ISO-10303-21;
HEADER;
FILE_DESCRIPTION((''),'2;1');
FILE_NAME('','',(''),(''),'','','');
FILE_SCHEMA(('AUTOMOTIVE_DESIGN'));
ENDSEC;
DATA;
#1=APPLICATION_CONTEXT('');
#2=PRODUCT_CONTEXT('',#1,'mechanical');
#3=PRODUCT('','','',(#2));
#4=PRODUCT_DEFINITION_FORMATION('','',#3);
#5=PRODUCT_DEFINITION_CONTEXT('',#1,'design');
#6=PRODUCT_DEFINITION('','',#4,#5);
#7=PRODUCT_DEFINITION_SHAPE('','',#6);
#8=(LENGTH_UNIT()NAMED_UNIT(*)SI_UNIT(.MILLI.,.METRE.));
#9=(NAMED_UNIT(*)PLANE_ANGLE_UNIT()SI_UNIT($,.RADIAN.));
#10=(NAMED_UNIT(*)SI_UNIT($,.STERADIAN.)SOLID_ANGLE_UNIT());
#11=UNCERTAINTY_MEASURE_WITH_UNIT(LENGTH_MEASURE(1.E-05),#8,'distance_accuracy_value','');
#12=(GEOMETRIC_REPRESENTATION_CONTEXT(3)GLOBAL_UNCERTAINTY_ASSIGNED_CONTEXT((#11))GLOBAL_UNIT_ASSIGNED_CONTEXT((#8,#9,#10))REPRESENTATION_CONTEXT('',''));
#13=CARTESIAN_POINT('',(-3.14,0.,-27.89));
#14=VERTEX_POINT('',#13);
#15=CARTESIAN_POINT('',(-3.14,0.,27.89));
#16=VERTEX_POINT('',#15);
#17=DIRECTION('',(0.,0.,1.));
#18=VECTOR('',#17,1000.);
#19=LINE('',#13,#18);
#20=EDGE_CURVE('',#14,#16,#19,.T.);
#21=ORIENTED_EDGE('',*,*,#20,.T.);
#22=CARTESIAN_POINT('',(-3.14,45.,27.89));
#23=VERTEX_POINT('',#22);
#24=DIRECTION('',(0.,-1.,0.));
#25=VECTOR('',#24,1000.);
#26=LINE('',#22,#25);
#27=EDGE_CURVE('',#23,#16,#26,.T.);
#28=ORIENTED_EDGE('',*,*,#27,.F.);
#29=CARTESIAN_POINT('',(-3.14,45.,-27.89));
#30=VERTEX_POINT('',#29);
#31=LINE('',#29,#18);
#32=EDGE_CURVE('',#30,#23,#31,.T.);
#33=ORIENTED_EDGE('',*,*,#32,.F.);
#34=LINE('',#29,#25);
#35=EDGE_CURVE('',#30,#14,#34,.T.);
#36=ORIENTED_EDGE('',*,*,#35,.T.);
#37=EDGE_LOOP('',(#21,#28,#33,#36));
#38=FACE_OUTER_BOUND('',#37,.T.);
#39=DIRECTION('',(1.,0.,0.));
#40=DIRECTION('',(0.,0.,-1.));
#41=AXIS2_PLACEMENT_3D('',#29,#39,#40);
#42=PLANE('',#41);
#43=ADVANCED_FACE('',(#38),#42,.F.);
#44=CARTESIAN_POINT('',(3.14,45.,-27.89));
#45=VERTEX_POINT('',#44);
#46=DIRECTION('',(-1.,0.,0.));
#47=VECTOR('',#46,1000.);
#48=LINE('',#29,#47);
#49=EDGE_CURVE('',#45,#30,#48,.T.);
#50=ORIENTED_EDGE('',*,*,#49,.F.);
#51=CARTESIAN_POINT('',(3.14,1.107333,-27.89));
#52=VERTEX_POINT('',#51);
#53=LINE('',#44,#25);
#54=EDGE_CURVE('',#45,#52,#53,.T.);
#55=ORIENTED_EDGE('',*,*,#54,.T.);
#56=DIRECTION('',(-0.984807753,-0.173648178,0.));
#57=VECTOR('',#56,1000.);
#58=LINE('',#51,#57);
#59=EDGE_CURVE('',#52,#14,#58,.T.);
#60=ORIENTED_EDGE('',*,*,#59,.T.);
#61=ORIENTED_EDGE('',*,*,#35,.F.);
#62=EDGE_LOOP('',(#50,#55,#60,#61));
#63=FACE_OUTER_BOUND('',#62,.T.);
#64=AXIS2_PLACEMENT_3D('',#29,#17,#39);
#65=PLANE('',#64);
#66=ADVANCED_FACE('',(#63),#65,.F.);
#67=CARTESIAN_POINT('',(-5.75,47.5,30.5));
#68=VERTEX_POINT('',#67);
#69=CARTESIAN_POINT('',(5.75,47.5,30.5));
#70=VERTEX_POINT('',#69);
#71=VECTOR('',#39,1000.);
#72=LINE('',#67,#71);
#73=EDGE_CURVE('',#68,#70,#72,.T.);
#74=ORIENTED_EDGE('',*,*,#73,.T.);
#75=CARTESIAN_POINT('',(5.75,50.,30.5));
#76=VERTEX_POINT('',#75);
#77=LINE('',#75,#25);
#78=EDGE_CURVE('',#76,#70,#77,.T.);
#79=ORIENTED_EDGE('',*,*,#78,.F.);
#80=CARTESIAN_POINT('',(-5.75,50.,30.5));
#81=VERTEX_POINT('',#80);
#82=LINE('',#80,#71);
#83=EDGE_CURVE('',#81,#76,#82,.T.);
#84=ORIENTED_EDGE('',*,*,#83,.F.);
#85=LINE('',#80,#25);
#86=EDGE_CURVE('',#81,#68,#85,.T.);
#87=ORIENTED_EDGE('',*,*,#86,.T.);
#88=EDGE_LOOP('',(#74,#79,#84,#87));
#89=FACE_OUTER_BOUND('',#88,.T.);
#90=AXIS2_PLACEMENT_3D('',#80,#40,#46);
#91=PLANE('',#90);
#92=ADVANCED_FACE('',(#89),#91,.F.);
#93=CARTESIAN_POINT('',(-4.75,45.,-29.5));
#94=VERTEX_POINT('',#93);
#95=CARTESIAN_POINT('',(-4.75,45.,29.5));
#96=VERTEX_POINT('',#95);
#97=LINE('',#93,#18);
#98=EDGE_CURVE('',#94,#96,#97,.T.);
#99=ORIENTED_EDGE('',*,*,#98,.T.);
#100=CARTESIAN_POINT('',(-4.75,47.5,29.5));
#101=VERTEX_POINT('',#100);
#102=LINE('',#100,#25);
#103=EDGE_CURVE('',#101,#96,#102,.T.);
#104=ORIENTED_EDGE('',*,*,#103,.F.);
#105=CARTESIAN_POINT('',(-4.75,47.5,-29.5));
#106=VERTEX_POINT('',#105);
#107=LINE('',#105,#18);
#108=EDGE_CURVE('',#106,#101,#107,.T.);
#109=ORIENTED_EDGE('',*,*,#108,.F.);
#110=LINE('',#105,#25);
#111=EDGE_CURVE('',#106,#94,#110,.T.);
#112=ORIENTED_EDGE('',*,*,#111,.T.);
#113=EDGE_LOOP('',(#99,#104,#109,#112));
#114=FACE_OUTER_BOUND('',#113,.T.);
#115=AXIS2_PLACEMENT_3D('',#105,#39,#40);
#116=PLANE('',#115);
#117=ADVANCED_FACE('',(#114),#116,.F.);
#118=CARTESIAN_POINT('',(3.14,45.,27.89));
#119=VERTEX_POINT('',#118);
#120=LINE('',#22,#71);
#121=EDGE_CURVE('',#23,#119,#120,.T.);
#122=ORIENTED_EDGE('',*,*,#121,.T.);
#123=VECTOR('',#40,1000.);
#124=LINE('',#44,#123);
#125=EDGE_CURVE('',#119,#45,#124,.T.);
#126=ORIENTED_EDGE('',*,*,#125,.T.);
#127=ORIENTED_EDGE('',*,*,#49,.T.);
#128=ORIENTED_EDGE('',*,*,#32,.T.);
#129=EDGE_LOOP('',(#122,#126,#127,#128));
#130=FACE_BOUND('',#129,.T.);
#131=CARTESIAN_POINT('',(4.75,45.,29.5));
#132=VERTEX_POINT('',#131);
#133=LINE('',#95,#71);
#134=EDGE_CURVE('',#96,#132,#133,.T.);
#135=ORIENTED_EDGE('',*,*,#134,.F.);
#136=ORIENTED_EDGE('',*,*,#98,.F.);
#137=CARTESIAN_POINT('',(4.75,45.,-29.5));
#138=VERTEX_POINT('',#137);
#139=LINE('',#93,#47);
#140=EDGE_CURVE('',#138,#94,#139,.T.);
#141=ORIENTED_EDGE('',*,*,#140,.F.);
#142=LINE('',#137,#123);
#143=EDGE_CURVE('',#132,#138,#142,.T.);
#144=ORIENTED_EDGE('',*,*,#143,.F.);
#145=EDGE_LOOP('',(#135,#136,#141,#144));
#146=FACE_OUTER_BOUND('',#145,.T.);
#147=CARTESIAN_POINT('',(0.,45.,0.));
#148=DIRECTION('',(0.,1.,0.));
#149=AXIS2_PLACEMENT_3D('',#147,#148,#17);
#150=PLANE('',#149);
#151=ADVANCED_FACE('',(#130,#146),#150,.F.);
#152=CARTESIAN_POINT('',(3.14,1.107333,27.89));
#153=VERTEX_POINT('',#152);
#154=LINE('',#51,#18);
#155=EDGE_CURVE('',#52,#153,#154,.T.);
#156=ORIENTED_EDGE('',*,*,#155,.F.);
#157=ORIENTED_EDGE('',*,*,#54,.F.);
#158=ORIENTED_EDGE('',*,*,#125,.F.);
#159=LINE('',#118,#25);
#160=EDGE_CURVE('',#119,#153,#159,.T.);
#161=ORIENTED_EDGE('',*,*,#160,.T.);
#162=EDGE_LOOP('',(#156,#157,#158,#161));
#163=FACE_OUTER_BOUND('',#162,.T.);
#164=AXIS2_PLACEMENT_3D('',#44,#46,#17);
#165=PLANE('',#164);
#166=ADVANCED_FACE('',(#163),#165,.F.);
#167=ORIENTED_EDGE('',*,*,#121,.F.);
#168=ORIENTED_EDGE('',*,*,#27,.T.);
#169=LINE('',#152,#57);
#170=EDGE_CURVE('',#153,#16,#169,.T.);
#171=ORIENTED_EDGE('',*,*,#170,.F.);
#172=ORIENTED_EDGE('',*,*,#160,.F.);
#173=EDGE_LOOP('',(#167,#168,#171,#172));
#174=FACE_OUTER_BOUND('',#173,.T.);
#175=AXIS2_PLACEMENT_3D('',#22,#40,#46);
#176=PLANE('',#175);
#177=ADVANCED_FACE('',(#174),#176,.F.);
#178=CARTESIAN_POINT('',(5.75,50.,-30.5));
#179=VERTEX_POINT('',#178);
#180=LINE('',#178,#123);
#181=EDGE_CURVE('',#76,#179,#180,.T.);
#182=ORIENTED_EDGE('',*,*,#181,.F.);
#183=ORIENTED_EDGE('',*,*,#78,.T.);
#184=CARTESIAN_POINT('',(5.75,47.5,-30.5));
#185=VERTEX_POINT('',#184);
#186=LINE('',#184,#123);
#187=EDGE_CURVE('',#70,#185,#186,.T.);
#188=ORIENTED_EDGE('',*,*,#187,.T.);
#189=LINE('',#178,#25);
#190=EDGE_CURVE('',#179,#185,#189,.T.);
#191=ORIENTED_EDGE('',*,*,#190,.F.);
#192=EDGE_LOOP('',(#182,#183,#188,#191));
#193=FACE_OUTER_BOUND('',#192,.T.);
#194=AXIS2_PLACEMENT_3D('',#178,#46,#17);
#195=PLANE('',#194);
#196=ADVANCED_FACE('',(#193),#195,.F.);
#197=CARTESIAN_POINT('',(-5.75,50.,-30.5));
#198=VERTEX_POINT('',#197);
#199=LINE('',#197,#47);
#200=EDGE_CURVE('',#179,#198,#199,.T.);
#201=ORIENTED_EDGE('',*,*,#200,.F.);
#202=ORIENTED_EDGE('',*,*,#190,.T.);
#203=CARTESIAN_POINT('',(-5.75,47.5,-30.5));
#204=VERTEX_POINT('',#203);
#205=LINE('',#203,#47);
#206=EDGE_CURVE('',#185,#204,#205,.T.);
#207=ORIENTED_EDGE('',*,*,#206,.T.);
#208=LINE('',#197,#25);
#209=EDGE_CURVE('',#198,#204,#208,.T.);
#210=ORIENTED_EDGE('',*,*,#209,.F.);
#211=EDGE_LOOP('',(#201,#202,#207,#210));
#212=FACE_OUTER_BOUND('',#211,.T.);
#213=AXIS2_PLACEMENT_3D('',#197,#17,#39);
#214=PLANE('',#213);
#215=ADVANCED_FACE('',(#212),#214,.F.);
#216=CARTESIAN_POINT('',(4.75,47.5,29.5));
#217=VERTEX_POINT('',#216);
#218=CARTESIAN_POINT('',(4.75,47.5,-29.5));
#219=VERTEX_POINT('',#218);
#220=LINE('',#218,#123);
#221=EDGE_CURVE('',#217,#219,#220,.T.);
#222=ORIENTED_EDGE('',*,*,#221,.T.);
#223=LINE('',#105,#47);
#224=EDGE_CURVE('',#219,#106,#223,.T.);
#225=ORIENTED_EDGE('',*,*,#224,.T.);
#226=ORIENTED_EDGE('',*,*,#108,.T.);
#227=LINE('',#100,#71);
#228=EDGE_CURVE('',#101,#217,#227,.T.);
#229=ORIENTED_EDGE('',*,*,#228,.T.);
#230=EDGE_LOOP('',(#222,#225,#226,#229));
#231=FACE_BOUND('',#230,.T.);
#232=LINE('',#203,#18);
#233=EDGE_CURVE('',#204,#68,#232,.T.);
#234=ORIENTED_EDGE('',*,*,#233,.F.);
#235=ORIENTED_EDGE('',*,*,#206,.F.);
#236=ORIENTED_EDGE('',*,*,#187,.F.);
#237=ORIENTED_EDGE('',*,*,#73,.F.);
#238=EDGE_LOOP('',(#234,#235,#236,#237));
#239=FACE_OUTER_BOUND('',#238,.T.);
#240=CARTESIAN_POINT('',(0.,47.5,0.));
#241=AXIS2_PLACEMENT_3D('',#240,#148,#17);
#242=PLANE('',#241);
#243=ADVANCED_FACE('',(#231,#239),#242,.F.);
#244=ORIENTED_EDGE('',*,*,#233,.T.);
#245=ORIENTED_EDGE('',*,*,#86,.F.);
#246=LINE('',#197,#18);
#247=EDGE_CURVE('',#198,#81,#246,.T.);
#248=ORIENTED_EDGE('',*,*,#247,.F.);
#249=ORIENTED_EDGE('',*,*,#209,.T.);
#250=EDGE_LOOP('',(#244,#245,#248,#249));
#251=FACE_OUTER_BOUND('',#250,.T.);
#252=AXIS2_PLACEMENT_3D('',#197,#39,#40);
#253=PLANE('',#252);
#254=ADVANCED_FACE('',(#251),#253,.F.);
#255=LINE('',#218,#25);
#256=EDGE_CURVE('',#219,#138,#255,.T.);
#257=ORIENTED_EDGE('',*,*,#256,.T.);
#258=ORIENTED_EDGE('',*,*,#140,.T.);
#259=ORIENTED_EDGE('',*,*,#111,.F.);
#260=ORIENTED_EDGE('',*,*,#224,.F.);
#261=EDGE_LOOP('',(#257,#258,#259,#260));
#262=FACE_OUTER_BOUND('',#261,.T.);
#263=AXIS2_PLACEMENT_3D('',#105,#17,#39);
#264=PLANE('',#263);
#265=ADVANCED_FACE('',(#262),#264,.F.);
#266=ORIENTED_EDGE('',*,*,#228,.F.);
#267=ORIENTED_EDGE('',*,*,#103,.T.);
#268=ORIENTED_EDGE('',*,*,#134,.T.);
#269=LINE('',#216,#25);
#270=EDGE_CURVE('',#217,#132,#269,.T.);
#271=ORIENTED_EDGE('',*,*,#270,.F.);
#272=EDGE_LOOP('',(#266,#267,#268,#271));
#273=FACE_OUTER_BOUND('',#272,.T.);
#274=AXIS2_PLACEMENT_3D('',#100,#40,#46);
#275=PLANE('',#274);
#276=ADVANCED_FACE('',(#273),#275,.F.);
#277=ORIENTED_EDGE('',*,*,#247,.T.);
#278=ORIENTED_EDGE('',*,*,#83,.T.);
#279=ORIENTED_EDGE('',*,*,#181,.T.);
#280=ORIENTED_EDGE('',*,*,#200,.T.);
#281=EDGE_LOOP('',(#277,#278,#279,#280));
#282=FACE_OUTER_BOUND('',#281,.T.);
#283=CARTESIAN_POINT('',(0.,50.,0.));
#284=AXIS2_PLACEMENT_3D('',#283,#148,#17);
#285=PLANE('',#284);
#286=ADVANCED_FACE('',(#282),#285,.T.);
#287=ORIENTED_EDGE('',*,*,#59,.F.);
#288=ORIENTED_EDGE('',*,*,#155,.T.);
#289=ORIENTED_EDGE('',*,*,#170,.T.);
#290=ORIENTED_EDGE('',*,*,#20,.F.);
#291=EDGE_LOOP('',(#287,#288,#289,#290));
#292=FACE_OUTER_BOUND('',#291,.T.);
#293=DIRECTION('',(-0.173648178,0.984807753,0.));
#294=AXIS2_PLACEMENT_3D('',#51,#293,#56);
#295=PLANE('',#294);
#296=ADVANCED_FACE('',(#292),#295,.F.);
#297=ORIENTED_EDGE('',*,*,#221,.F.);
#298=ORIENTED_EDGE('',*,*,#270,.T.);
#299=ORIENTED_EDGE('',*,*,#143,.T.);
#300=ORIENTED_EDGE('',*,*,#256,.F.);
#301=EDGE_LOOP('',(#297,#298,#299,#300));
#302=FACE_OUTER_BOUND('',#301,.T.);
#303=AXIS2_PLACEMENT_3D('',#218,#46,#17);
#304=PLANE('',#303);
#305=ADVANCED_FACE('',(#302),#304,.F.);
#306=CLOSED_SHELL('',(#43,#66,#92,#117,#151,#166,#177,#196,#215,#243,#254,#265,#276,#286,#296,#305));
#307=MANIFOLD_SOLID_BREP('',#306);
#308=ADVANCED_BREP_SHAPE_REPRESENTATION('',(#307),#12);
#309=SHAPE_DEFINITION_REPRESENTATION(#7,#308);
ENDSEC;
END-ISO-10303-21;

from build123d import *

# Parameters (mm, degrees)
SKETCH1_W           = 6.28
SKETCH1_H           = 55.78
BOSS_EXTRUDE1_DEPTH = 45
CUT_EXTRUDE1_DEPTH  = 72.737493684
SKETCH3_W           = 9.5
SKETCH3_H           = 59
BOSS_EXTRUDE2_DEPTH = 2.5
SKETCH4_W           = 11.5
SKETCH4_H           = 61
BOSS_EXTRUDE3_DEPTH = 2.5


with BuildPart() as part:
    # Sketch1 → Boss-Extrude1 (new body)
    with BuildSketch(Plane(origin=(0, 0, 0), x_dir=(1, 0, 0), z_dir=(0, 1, 0))):
        Rectangle(SKETCH1_W, SKETCH1_H)
    extrude(amount=BOSS_EXTRUDE1_DEPTH)

    # Sketch2 → Cut-Extrude1 (cut, through all)
    with BuildSketch(Plane.XY.offset(27.89)):
        Polygon((-3.14, 0), (3.14, 0), (3.14, 1.107333439), align=None)
    extrude(amount=-CUT_EXTRUDE1_DEPTH, mode=Mode.SUBTRACT)

    # Sketch3 → Boss-Extrude2 (add)
    with BuildSketch(Plane(origin=(0, 45, 0), x_dir=(1, 0, 0), z_dir=(0, 1, 0))):
        Rectangle(SKETCH3_W, SKETCH3_H)
    extrude(amount=BOSS_EXTRUDE2_DEPTH)

    # Sketch4 → Boss-Extrude3 (add)
    with BuildSketch(Plane(origin=(0, 47.5, 0), x_dir=(1, 0, 0), z_dir=(0, 1, 0))):
        Rectangle(SKETCH4_W, SKETCH4_H)
    extrude(amount=BOSS_EXTRUDE3_DEPTH)


solid = part.part
